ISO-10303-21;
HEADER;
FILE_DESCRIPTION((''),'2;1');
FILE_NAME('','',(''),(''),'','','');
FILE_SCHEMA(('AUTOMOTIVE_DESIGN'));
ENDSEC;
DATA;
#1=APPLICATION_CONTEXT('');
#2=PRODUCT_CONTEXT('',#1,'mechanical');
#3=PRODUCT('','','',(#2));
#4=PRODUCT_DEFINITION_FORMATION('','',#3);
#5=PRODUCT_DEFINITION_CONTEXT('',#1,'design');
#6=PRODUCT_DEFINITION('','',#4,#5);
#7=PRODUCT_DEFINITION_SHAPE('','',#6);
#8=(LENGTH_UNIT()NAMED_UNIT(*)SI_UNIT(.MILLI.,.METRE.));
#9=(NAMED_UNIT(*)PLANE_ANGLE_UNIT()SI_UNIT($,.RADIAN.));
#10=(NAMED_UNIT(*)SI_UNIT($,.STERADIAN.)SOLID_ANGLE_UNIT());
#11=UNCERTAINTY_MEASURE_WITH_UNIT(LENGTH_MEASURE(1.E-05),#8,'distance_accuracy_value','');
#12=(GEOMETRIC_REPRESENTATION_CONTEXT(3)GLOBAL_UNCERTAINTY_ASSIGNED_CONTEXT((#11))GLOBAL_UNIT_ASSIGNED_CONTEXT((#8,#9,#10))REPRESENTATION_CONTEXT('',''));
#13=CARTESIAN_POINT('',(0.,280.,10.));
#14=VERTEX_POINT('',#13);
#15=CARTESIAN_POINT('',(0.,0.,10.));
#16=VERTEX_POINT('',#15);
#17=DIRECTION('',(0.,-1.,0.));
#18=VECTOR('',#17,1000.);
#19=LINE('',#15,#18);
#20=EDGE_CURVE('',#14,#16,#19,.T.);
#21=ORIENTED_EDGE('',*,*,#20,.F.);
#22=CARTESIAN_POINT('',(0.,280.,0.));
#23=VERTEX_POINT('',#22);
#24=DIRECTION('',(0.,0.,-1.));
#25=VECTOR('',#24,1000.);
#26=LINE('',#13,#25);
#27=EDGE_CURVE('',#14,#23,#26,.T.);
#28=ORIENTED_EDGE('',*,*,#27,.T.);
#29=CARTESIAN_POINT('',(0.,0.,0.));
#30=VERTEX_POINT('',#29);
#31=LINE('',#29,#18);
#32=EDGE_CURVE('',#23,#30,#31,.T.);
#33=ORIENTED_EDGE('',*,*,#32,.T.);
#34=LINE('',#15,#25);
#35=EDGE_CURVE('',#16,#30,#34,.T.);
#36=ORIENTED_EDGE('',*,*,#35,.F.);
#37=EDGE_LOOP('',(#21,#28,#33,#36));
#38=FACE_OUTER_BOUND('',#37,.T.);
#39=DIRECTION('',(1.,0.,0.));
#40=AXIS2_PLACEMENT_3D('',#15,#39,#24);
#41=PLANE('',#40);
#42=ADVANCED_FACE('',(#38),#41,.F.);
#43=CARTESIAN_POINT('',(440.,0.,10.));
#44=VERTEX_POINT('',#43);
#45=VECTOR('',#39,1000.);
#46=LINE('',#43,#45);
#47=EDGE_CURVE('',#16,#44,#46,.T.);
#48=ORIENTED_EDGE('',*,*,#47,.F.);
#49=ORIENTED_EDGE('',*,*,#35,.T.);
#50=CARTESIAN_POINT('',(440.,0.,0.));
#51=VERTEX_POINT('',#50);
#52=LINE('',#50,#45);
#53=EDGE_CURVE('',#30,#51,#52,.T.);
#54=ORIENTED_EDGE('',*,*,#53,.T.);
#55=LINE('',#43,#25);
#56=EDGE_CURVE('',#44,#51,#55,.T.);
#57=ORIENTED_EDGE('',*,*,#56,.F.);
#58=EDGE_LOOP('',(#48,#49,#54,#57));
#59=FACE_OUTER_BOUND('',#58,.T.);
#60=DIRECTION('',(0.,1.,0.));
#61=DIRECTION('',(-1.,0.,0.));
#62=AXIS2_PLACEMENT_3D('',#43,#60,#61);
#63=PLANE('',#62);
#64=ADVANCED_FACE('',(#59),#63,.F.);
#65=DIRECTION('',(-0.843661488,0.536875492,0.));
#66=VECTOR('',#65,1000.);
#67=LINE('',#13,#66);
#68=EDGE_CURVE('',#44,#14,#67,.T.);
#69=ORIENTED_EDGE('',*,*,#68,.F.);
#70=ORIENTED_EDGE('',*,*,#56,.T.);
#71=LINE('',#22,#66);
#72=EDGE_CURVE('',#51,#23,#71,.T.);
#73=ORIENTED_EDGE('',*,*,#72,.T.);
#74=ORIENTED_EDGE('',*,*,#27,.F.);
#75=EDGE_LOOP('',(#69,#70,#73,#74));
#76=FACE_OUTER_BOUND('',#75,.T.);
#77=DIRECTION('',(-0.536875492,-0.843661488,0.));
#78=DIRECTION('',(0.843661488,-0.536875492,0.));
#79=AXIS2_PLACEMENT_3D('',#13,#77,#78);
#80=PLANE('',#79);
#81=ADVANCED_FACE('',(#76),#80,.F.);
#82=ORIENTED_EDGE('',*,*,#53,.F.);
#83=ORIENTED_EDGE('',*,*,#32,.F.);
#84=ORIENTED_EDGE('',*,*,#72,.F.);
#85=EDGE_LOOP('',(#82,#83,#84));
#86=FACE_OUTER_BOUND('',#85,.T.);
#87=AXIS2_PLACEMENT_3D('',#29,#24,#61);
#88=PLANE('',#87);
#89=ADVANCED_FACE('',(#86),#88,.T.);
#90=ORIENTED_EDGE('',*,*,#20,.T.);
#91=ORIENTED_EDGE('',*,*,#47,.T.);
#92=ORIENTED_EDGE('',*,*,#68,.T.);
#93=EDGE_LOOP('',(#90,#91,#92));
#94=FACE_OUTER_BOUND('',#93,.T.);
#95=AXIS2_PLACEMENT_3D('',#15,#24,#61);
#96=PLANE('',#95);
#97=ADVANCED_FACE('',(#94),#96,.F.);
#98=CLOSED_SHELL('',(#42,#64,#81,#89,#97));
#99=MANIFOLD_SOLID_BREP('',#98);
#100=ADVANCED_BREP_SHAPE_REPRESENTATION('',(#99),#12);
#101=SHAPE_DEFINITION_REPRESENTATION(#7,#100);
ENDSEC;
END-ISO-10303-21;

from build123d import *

# Parameters (mm, degrees)
BOSS_EXTRUDE1_DEPTH = 10


with BuildPart() as part:
    # Sketch1 → Boss-Extrude1 (new body)
    with BuildSketch(Plane.XY):
        Polygon((0, 0), (0, 280), (440, 0), align=None)
    extrude(amount=BOSS_EXTRUDE1_DEPTH)


solid = part.part
